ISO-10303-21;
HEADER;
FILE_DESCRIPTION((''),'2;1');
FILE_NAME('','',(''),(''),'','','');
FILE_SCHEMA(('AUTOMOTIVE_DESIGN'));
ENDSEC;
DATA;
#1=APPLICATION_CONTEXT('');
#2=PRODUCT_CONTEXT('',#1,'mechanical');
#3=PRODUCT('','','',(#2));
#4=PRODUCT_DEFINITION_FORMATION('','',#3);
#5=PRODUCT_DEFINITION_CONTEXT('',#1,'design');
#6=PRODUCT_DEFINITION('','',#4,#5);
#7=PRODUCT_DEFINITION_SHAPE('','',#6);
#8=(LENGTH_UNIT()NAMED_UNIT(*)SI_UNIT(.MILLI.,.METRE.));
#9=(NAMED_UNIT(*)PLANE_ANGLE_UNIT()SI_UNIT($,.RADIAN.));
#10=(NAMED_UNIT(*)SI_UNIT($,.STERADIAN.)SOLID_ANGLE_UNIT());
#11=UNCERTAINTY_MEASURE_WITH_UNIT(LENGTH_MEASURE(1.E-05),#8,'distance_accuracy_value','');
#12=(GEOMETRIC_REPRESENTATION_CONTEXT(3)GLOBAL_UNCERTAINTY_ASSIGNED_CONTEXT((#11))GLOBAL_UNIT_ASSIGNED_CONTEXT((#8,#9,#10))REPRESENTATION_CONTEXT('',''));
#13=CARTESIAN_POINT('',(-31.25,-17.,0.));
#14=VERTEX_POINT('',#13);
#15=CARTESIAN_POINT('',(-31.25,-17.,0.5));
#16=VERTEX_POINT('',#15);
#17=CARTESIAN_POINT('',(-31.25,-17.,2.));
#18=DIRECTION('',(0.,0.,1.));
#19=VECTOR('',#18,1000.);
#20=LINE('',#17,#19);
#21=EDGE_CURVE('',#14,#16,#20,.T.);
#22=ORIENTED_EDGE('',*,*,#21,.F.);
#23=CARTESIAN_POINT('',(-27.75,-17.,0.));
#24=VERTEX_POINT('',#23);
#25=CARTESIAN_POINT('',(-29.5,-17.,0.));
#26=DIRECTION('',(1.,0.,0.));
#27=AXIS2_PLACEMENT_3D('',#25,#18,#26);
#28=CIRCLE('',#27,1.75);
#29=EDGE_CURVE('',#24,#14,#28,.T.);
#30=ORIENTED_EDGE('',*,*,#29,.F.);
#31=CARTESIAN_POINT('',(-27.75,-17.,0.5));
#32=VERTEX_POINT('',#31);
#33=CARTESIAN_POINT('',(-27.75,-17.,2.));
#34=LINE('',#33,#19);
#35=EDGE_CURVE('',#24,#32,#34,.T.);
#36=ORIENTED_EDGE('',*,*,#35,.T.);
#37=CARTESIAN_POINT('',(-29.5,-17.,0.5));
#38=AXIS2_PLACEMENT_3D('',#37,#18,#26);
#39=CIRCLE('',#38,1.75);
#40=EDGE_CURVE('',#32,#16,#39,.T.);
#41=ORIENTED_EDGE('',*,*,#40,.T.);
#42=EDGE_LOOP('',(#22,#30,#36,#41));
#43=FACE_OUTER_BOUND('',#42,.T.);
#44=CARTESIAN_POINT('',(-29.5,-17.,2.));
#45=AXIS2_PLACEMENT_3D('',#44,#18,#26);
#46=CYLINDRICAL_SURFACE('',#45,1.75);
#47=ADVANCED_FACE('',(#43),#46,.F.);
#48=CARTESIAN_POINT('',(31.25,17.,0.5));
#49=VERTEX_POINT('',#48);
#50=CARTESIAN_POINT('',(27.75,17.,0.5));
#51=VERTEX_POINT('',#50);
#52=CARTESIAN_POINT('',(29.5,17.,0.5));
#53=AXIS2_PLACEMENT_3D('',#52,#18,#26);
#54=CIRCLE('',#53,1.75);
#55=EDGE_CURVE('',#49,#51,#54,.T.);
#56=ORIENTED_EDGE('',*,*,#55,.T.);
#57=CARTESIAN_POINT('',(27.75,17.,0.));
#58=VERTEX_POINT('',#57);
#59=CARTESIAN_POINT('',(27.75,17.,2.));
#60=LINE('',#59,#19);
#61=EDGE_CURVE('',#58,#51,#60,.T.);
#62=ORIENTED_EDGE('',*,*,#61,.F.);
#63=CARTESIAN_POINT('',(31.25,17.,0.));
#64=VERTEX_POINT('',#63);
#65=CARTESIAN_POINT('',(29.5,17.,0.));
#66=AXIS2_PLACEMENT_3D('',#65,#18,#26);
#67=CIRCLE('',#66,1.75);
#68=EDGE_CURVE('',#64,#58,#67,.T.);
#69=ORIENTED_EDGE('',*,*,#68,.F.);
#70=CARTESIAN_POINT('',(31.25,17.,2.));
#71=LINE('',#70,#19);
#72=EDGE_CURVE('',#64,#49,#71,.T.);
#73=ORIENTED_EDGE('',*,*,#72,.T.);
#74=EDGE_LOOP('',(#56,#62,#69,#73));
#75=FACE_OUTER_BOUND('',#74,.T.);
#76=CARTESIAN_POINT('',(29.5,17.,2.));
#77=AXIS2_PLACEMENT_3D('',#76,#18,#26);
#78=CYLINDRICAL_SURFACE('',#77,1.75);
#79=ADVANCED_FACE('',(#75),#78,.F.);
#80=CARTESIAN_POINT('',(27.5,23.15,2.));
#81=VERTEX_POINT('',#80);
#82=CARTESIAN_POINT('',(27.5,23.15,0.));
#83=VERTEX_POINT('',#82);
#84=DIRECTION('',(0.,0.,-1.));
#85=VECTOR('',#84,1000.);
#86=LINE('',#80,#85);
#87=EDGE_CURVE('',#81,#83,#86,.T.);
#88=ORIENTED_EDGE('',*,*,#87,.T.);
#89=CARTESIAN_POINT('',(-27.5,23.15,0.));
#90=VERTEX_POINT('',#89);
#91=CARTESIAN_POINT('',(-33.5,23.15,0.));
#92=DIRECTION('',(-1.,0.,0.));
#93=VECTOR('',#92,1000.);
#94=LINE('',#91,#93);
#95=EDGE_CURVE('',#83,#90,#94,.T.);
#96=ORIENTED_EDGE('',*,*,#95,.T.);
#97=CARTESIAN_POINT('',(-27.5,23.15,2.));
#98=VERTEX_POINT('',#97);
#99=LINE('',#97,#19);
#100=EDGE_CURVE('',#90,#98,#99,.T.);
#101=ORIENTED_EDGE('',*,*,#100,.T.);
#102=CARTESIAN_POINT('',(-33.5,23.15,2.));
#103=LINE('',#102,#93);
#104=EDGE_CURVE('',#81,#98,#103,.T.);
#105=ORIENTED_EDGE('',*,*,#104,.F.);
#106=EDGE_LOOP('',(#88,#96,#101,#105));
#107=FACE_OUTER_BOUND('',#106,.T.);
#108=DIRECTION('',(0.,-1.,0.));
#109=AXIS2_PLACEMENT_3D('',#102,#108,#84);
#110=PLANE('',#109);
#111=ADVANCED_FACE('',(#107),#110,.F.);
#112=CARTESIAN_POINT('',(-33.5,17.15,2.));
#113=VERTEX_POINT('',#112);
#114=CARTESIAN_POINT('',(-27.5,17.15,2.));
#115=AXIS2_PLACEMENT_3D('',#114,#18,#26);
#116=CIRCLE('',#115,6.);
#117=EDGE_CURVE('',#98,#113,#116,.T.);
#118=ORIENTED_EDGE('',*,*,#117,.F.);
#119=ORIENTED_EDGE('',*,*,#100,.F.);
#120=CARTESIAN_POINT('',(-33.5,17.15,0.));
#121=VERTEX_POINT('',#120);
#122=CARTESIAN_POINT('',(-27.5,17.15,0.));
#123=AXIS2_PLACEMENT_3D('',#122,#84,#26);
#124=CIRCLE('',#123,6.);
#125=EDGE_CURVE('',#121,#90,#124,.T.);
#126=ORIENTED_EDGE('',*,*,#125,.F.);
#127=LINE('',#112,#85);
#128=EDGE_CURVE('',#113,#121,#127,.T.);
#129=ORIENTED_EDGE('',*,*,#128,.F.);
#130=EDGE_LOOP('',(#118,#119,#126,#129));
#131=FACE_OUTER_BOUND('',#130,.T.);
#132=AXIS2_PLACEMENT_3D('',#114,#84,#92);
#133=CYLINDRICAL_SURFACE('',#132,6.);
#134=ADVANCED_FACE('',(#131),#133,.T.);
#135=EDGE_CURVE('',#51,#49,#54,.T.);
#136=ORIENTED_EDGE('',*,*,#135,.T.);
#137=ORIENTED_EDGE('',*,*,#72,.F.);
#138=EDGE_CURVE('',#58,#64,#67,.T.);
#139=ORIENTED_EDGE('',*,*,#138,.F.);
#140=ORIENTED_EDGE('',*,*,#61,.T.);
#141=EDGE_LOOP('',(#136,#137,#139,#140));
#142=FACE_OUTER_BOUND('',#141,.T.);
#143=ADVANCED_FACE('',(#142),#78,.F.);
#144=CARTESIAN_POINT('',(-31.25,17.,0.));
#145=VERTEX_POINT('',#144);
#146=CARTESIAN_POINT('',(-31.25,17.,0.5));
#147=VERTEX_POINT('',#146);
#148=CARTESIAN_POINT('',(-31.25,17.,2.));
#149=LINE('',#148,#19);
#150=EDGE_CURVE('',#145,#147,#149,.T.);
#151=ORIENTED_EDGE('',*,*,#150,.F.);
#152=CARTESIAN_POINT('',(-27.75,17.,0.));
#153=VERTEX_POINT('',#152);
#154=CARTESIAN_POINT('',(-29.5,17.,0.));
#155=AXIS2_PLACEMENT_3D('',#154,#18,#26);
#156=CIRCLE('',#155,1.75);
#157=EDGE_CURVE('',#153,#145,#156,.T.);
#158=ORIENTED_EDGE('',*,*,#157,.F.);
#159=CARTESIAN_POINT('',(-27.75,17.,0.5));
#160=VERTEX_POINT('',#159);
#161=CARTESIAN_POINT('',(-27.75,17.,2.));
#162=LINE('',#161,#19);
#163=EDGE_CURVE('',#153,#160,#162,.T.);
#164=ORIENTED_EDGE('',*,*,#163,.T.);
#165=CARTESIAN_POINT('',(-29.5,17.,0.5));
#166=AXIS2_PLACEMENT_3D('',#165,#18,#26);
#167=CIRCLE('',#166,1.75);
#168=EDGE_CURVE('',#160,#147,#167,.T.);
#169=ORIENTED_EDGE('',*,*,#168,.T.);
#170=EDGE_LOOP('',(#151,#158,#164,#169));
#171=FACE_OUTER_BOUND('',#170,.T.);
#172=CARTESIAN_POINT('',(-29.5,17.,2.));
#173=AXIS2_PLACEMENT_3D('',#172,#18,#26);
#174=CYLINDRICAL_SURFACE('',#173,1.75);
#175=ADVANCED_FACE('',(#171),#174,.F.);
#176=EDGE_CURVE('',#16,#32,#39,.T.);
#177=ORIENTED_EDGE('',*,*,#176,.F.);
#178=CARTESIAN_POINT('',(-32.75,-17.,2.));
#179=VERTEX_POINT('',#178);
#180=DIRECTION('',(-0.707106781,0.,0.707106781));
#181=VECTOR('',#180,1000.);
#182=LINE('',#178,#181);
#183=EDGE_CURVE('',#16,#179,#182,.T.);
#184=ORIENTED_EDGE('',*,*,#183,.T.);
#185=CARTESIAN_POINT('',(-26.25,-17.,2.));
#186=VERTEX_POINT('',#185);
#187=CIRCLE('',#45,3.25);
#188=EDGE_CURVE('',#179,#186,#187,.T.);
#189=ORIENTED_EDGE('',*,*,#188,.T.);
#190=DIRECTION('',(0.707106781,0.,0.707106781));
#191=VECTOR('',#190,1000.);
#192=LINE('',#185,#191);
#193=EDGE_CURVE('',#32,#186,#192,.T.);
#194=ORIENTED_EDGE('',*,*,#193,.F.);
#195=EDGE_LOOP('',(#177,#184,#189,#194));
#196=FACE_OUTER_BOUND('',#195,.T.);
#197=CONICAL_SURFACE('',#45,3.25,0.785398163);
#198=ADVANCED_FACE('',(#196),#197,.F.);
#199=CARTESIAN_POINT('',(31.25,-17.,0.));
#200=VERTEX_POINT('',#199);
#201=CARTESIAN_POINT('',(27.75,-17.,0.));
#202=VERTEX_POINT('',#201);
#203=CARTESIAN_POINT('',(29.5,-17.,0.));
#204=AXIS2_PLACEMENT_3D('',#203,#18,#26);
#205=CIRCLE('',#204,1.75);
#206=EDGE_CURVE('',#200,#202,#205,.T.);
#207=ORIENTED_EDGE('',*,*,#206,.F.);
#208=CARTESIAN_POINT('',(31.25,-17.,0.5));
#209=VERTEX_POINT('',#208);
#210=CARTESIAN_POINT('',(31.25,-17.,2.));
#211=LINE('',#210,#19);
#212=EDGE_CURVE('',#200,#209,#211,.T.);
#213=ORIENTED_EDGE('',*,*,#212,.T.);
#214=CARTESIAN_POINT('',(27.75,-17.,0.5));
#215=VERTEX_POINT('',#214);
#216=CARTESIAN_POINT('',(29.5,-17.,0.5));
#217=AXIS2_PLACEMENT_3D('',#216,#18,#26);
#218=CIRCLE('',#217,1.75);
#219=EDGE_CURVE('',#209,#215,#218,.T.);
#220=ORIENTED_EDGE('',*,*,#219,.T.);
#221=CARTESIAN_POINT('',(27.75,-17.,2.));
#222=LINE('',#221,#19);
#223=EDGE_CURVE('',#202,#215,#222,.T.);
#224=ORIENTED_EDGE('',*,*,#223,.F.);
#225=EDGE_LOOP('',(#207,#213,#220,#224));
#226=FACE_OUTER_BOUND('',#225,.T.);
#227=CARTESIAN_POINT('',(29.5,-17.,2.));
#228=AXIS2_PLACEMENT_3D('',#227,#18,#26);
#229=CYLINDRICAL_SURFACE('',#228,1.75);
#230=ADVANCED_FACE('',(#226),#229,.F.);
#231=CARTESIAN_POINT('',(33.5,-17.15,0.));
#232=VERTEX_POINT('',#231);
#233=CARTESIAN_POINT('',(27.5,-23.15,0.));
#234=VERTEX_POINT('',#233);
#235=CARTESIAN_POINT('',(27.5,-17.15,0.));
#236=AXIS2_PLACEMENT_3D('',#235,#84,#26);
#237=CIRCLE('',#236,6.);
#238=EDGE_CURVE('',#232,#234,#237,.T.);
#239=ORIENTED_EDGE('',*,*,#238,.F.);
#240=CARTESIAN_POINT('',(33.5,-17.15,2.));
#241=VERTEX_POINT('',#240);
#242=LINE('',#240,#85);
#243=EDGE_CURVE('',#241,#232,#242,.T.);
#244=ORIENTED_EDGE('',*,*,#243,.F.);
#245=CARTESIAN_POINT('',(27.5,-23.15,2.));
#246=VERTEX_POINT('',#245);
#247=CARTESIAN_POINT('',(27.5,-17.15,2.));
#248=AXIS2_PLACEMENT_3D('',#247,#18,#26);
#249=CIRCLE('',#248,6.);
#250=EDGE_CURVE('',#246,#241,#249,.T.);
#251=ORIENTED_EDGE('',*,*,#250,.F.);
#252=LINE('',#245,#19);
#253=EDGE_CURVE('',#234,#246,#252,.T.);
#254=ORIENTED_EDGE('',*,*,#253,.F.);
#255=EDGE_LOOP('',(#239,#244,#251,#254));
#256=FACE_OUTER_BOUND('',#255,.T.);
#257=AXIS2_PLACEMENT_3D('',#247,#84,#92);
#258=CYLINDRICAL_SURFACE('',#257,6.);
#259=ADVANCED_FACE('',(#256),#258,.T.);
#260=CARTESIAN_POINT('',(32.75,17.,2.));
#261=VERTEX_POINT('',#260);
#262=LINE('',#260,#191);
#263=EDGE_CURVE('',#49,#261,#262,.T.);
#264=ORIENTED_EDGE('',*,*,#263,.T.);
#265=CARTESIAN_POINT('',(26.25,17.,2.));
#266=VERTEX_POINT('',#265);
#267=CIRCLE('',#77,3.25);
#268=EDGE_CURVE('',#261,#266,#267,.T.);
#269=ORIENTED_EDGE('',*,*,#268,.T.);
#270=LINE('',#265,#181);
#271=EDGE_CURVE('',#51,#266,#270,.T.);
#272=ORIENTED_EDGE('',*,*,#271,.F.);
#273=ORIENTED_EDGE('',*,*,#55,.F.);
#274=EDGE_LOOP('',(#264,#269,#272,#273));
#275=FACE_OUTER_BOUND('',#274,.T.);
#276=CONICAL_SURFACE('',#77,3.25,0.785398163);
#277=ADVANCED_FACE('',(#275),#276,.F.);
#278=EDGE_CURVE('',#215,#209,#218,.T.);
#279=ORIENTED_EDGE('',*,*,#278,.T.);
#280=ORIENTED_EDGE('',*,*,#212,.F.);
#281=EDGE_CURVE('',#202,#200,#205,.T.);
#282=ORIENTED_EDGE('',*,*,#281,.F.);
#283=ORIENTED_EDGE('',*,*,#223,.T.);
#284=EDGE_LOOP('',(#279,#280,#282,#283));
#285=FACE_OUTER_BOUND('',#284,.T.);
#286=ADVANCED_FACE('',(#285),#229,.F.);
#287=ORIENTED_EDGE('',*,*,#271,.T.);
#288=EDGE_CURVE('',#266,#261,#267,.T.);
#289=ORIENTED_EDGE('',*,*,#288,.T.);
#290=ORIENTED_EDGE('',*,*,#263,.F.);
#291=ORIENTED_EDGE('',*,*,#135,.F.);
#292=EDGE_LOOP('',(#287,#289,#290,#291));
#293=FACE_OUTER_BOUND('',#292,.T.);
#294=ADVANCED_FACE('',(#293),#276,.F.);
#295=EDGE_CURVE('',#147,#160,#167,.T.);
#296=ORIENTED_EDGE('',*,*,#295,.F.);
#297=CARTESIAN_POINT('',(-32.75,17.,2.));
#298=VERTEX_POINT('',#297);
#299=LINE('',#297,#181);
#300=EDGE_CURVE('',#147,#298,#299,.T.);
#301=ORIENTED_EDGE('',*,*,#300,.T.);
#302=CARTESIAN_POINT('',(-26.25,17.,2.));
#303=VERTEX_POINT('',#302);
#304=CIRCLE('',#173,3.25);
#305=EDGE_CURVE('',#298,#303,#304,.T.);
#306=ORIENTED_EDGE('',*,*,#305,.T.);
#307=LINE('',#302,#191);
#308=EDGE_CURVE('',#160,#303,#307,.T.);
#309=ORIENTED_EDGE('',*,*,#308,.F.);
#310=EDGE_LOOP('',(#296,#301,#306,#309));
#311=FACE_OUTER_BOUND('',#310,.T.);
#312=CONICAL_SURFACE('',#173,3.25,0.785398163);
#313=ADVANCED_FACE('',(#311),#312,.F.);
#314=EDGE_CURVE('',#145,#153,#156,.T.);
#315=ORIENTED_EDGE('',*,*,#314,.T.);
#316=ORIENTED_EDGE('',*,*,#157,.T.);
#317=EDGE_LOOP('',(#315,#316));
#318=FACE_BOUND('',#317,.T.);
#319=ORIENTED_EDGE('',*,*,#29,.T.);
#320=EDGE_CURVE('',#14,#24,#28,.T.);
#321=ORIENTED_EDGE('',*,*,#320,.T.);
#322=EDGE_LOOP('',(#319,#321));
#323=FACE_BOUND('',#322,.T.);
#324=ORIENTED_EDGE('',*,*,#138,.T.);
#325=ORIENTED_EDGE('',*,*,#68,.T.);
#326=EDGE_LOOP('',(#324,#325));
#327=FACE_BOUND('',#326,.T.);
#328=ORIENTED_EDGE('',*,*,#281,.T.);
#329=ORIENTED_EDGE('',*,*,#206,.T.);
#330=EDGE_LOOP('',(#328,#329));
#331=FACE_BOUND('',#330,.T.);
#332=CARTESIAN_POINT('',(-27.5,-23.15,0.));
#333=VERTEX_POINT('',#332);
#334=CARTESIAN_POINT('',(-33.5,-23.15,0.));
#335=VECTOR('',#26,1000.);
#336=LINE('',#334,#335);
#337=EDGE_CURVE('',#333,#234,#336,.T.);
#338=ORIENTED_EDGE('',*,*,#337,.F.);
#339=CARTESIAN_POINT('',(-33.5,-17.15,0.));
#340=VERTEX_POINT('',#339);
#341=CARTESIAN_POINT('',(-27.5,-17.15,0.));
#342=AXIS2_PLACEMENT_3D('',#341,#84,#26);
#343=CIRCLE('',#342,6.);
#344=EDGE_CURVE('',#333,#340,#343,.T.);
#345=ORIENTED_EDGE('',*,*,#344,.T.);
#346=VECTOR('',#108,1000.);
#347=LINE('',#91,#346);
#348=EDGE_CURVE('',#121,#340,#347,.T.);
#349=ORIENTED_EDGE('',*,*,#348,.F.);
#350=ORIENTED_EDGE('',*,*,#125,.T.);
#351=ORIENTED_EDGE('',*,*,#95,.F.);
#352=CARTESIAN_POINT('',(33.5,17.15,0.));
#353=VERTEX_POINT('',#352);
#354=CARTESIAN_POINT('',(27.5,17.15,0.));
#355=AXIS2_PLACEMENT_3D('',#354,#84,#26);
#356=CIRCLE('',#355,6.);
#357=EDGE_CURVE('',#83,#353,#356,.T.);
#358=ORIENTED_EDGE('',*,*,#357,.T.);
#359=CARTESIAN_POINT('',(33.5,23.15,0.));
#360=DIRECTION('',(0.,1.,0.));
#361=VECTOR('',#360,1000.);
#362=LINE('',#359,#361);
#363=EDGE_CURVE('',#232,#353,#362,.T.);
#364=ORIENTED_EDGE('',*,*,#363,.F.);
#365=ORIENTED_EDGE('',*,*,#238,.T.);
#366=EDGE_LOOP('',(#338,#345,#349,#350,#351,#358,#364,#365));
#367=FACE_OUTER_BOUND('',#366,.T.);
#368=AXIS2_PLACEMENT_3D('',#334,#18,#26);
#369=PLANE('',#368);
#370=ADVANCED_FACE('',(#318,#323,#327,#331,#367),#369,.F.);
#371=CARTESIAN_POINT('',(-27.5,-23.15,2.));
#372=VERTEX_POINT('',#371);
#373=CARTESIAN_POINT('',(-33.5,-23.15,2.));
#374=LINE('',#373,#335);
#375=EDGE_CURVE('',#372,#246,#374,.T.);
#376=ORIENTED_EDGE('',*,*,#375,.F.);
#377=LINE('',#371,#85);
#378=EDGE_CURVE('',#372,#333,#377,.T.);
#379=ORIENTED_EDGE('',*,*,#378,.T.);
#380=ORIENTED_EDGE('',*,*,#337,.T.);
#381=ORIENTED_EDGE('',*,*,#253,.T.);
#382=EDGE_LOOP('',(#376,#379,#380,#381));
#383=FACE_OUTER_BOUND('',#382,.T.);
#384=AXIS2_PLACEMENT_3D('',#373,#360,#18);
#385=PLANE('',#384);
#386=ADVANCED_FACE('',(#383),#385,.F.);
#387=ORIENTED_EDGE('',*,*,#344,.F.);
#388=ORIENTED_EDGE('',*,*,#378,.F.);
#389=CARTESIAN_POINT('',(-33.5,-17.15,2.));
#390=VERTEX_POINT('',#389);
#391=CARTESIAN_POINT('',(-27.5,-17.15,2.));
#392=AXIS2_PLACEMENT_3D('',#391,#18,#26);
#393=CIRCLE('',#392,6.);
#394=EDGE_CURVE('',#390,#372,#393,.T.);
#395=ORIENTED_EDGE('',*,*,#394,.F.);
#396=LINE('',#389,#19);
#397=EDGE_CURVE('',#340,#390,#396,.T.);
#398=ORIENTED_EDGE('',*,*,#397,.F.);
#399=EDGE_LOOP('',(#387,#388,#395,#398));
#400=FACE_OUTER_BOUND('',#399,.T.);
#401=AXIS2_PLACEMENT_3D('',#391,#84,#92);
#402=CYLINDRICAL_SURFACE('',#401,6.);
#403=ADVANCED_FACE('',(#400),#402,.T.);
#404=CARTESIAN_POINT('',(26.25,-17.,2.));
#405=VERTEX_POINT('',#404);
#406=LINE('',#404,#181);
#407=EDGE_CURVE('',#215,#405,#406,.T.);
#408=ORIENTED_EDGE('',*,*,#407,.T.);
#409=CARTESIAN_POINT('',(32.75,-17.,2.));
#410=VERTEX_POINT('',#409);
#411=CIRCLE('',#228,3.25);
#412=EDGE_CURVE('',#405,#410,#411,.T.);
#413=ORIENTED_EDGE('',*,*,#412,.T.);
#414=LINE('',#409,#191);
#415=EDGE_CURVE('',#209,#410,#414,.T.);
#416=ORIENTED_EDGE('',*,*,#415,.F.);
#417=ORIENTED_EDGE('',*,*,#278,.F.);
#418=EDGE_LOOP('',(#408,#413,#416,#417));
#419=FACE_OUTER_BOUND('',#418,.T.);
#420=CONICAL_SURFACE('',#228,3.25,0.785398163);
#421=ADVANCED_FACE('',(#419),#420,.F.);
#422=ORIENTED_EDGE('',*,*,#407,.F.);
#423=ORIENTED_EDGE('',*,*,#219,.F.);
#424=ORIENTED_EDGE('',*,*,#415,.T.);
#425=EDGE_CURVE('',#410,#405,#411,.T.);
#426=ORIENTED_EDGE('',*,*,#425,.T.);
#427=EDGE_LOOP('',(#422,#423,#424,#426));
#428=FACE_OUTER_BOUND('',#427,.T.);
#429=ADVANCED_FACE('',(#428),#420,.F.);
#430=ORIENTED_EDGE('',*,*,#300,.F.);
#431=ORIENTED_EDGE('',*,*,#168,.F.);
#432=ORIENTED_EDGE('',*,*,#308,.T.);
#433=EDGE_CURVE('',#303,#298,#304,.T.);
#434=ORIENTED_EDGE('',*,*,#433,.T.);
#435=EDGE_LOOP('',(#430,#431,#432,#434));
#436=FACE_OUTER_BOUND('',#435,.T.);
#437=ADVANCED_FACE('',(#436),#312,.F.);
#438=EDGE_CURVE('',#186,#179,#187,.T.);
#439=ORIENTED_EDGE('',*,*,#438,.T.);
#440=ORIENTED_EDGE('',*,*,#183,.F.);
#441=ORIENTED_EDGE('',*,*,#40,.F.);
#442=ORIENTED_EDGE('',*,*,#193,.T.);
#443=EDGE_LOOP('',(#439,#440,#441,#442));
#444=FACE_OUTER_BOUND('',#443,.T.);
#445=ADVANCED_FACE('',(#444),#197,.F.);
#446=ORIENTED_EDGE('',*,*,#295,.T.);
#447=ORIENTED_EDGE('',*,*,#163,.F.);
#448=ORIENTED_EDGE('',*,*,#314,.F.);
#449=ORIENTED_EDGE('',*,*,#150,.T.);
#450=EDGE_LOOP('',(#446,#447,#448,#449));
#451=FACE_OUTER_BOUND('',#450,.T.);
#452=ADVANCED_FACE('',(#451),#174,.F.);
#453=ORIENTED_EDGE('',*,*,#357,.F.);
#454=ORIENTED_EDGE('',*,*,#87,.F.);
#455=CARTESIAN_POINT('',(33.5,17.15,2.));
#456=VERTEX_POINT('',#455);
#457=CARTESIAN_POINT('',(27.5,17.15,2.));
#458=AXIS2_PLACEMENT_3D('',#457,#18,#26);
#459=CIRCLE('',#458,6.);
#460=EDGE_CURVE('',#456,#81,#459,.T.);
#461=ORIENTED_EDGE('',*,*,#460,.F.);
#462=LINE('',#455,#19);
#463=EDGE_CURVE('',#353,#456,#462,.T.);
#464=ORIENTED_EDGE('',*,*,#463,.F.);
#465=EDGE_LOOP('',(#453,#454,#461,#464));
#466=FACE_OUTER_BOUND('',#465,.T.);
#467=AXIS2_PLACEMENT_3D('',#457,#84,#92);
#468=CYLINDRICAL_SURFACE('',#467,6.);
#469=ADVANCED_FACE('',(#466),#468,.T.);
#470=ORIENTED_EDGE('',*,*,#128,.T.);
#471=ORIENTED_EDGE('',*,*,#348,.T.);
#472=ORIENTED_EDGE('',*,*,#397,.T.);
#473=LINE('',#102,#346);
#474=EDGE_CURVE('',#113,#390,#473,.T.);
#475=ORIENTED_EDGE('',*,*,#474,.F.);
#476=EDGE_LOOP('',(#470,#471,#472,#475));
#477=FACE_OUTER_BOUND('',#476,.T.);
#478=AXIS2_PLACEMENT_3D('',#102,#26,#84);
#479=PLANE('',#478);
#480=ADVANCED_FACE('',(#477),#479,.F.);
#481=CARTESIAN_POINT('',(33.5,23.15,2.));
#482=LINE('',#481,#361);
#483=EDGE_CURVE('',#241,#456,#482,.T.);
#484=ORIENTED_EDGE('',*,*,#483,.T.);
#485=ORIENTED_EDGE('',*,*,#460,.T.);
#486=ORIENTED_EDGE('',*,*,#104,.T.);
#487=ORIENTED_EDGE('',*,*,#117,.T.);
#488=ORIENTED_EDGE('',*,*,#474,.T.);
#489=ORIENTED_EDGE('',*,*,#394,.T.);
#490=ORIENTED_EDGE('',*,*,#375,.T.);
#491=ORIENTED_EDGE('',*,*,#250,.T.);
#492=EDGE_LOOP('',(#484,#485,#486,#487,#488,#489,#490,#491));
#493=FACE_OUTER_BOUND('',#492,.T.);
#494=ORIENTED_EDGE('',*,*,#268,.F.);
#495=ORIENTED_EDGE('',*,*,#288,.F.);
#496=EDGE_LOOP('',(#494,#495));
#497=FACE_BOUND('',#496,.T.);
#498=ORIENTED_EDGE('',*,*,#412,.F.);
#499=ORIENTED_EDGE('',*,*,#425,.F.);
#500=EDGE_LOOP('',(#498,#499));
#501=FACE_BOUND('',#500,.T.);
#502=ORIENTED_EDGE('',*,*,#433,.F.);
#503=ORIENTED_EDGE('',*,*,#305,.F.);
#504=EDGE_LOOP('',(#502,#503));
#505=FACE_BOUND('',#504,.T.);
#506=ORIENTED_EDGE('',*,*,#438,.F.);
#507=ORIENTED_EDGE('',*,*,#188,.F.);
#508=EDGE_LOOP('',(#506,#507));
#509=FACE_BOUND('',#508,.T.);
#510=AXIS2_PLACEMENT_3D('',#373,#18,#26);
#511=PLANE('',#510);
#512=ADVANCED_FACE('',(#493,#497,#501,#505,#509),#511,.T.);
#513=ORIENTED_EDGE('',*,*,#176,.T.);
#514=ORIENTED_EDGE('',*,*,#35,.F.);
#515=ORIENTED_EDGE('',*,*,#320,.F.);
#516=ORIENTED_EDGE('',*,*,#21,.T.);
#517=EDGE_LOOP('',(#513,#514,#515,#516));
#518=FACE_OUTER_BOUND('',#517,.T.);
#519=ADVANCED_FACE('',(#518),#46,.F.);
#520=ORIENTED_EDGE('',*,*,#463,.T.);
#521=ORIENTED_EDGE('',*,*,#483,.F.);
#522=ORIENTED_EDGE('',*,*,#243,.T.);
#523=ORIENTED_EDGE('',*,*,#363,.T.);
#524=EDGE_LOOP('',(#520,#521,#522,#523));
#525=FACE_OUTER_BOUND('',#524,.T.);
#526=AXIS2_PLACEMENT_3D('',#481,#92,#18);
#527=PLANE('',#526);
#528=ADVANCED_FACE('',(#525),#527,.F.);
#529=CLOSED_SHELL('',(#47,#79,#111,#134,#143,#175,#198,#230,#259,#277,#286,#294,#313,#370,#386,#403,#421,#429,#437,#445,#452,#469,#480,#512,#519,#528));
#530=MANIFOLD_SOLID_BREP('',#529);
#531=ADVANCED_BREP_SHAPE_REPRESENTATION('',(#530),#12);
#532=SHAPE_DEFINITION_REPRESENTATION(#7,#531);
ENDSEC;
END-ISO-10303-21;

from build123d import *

# Parameters (mm, degrees)
SKETCH_1_W                  = 67
SKETCH_1_H                  = 46.3
EXTRUDE_1_DEPTH             = 2
FILLET_1_R                  = 6
HOLE_WIZARD_1_D             = 3.5
HOLE_WIZARD_1_DEPTH         = 10
HOLE_WIZARD_1_CSINK_D       = 6.5
HOLE_WIZARD_1_CSINK_ANGLE   = 90
PATTERN_LINEAR_1_COUNT      = 2
PATTERN_LINEAR_1_PITCH      = 34
PATTERN_LINEAR_1_COUNT_DIR2 = 2
PATTERN_LINEAR_1_PITCH_DIR2 = 59


with BuildPart() as part:
    # 草图1 → 拉伸1 (new body)
    with BuildSketch(Plane.XY):
        Rectangle(SKETCH_1_W, SKETCH_1_H)
    extrude(amount=EXTRUDE_1_DEPTH)

    # 圆角1
    fillet_1_edges = [part.edges().sort_by_distance(p)[0] for p in [
        (-33.5, 23.15, 1),
        (33.5, 23.15, 1),
        (33.5, -23.15, 1),
        (-33.5, -23.15, 1),
    ]]
    fillet(fillet_1_edges, radius=FILLET_1_R)

    # 孔1
    with Locations(Plane(origin=(-29.5, -17, 2), x_dir=(1, 0, 0), z_dir=(0, 0, 1))):
        with Locations((0, 0)):
            hole_wizard_1 = CounterSinkHole(HOLE_WIZARD_1_D / 2, HOLE_WIZARD_1_CSINK_D / 2, depth=HOLE_WIZARD_1_DEPTH, counter_sink_angle=HOLE_WIZARD_1_CSINK_ANGLE)

    # 阵列(线性)1: Hole Wizard 1 2 × 2
    with Locations(*[(j * PATTERN_LINEAR_1_PITCH_DIR2, i * PATTERN_LINEAR_1_PITCH, 0) for i in range(PATTERN_LINEAR_1_COUNT) for j in range(PATTERN_LINEAR_1_COUNT_DIR2) if (i, j) != (0, 0)]):
        add(hole_wizard_1, mode=Mode.SUBTRACT)


solid = part.part
